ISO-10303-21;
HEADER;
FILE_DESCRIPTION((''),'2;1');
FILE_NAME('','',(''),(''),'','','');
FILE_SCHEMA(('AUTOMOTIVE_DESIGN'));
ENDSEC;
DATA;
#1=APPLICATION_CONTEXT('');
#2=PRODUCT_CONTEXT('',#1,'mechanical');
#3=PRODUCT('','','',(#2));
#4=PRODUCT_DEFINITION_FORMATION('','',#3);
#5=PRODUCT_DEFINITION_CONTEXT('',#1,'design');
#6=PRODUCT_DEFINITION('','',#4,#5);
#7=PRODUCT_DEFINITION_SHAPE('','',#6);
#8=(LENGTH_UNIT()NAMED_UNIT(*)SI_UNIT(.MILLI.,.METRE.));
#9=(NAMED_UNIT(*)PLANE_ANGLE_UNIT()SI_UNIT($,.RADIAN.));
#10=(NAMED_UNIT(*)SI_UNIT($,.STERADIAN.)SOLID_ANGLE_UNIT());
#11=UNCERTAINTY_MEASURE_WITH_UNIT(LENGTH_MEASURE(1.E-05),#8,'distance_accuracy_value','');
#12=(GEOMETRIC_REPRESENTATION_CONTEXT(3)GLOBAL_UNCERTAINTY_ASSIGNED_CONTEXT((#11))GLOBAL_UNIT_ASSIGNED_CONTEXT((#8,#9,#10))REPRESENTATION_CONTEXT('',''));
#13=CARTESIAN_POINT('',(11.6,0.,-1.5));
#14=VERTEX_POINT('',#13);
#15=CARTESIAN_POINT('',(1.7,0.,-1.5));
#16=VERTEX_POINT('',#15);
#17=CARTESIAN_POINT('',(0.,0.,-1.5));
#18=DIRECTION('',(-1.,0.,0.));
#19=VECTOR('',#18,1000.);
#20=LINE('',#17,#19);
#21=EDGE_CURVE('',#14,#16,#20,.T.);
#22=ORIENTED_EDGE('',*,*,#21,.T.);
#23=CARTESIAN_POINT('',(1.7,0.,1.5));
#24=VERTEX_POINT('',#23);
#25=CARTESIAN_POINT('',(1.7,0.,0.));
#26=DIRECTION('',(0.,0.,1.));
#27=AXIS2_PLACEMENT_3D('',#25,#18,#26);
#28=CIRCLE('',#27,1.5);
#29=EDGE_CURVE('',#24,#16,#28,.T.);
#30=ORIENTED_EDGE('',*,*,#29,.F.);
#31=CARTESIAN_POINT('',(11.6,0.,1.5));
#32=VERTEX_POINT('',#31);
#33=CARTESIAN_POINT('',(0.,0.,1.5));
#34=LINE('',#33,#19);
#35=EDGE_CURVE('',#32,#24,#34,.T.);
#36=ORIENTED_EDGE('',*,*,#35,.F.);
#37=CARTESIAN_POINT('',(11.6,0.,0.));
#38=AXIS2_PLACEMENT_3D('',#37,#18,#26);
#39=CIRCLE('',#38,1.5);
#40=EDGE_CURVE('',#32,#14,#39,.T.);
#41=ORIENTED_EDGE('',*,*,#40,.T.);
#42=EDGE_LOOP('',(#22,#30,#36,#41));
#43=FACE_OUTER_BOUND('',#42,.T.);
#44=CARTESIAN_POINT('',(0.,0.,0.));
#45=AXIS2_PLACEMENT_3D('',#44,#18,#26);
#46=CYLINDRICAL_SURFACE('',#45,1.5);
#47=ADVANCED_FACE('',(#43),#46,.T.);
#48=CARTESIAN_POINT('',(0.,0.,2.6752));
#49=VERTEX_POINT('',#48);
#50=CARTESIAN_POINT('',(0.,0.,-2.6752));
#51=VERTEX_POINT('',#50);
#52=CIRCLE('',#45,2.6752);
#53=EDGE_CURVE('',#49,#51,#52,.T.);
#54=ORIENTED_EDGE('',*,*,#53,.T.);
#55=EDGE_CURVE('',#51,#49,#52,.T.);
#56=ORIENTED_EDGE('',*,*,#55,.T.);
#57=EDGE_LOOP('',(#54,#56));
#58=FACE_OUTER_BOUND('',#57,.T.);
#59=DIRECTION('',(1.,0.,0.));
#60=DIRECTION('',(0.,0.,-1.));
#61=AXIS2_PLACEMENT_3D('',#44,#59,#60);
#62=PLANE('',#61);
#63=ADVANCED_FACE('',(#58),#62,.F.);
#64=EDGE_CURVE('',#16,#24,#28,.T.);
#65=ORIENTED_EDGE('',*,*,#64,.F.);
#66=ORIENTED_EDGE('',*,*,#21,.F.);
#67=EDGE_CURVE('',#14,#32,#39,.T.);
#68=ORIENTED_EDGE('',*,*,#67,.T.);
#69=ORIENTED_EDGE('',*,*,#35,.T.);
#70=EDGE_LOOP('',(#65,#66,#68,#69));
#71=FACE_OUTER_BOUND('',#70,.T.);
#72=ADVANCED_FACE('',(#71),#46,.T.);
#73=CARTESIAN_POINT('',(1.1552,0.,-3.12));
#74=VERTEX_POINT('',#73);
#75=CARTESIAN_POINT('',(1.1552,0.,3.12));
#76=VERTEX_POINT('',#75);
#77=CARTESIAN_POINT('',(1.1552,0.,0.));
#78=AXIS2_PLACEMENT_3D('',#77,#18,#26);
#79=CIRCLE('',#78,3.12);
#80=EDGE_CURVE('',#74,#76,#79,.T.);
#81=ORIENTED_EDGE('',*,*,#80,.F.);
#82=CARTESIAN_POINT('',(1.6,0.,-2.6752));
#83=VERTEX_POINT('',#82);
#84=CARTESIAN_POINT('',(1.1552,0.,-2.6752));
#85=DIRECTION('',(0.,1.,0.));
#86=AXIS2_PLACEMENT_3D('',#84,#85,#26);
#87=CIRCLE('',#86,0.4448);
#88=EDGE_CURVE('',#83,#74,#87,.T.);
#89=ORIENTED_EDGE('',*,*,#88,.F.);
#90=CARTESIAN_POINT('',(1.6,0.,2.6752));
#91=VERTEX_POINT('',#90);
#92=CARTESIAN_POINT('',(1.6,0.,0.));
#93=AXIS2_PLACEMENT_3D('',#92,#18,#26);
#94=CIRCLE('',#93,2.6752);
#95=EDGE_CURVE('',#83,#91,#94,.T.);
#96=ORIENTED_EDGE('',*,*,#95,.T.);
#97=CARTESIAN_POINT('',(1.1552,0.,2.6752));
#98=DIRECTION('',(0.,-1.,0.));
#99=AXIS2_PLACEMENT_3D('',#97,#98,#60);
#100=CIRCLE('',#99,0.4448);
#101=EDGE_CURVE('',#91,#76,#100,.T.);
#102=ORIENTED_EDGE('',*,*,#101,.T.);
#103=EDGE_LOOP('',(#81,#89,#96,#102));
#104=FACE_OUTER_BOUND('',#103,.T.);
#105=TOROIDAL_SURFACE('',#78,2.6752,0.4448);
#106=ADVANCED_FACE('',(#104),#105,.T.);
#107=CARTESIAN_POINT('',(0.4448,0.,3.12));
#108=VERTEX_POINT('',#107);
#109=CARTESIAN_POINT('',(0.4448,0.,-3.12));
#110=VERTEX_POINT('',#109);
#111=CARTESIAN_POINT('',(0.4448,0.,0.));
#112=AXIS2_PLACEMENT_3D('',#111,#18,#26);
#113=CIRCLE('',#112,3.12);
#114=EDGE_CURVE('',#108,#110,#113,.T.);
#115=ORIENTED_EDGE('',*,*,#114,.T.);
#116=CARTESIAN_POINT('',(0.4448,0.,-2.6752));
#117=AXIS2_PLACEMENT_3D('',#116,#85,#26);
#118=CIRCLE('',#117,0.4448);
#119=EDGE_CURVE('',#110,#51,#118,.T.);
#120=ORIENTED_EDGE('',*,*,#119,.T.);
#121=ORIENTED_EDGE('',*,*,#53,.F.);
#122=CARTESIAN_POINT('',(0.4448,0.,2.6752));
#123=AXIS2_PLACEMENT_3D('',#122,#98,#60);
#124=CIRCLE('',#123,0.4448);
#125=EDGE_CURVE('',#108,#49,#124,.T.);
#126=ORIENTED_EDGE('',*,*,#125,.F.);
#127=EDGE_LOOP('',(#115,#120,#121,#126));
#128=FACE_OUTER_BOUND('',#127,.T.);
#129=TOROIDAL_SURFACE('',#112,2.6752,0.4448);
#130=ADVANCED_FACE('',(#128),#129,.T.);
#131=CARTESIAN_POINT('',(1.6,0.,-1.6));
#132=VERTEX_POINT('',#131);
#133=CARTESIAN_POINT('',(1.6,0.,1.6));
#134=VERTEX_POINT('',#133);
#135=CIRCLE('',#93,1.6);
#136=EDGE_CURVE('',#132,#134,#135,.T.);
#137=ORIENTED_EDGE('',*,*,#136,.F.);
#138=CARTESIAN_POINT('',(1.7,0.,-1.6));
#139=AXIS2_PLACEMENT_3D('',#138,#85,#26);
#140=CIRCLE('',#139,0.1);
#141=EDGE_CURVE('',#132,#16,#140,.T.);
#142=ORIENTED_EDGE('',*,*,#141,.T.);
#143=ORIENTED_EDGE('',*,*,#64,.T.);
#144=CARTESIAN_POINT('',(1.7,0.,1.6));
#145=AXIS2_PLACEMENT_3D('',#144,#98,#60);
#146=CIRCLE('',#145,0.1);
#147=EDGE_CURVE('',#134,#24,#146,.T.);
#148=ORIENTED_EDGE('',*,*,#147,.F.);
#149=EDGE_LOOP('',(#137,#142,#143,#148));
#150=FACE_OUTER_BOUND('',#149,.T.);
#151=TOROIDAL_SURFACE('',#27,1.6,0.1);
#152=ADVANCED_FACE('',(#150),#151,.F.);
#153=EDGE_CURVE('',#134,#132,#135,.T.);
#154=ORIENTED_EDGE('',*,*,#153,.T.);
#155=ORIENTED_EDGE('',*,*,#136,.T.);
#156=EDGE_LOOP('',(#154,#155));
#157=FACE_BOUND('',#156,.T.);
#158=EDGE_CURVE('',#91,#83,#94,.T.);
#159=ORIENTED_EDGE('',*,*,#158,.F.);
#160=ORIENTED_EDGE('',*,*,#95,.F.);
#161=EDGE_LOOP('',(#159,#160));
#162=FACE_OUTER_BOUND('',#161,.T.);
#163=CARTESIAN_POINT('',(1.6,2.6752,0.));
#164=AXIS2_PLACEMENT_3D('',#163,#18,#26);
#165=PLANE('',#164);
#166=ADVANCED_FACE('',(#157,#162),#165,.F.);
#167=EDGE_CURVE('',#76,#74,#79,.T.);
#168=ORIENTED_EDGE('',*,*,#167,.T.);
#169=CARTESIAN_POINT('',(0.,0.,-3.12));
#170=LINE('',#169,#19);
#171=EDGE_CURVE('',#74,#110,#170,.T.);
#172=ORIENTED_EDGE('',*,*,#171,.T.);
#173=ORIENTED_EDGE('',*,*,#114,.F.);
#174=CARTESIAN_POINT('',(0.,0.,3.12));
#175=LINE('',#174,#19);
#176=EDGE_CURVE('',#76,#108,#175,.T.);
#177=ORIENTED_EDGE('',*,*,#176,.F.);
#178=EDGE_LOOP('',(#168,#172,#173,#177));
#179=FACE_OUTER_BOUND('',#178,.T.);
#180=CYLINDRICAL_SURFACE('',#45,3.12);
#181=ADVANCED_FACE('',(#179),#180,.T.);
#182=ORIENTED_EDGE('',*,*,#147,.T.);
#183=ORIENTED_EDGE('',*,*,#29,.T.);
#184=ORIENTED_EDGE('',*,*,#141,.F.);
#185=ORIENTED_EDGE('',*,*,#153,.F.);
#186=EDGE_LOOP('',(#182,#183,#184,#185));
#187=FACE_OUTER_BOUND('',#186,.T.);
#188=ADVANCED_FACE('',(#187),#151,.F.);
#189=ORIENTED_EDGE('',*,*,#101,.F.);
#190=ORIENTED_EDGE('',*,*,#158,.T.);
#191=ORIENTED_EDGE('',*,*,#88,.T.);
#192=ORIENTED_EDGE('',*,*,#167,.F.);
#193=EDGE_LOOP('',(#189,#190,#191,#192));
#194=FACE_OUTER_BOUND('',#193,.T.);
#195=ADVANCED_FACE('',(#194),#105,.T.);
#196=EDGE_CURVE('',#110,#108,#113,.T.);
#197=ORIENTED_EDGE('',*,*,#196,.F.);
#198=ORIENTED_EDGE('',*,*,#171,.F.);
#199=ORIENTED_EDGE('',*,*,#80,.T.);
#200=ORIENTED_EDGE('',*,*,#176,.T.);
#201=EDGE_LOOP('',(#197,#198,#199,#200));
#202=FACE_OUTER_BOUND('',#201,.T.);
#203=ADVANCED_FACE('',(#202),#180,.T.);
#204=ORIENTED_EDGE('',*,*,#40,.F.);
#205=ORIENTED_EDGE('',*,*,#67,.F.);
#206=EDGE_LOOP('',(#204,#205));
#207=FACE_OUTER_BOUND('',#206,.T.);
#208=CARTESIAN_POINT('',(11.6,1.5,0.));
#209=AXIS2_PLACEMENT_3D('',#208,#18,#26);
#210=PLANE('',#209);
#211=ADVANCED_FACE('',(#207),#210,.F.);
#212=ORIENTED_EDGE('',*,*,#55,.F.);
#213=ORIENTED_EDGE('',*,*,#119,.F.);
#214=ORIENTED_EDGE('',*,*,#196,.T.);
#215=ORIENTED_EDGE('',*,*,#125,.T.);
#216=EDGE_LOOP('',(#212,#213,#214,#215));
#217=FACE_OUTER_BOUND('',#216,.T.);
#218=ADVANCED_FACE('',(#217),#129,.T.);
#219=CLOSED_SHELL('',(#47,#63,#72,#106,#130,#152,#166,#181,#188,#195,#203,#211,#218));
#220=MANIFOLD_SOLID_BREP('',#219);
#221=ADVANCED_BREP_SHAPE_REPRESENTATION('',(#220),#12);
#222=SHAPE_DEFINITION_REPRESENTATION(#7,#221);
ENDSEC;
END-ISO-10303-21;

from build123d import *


with BuildPart() as part:
    # Dimensioned Sketch → Revolve3 (revolve)
    with BuildSketch(Plane.XY, mode=Mode.PRIVATE) as revolve3_sk:
        with BuildLine():
            Line((0, 0), (0, 2.6752))
            ThreePointArc((0, 2.6752), (0.130278904, 2.989721096), (0.4448, 3.12))
            Line((0.4448, 3.12), (1.1552, 3.12))
            ThreePointArc((1.1552, 3.12), (1.469721096, 2.989721096), (1.6, 2.6752))
            Line((1.6, 2.6752), (1.6, 1.6))
            ThreePointArc((1.6, 1.6), (1.629289322, 1.529289322), (1.7, 1.5))
            Line((1.7, 1.5), (11.6, 1.5))
            Line((11.6, 1.5), (11.6, 0))
            Line((11.6, 0), (0, 0))
        make_face()
    revolve(revolve3_sk.sketch.rotate(Axis((0, 0, 0), (1, 0, 0)), 90), axis=Axis((0, 0, 0), (1, 0, 0)))


solid = part.part
